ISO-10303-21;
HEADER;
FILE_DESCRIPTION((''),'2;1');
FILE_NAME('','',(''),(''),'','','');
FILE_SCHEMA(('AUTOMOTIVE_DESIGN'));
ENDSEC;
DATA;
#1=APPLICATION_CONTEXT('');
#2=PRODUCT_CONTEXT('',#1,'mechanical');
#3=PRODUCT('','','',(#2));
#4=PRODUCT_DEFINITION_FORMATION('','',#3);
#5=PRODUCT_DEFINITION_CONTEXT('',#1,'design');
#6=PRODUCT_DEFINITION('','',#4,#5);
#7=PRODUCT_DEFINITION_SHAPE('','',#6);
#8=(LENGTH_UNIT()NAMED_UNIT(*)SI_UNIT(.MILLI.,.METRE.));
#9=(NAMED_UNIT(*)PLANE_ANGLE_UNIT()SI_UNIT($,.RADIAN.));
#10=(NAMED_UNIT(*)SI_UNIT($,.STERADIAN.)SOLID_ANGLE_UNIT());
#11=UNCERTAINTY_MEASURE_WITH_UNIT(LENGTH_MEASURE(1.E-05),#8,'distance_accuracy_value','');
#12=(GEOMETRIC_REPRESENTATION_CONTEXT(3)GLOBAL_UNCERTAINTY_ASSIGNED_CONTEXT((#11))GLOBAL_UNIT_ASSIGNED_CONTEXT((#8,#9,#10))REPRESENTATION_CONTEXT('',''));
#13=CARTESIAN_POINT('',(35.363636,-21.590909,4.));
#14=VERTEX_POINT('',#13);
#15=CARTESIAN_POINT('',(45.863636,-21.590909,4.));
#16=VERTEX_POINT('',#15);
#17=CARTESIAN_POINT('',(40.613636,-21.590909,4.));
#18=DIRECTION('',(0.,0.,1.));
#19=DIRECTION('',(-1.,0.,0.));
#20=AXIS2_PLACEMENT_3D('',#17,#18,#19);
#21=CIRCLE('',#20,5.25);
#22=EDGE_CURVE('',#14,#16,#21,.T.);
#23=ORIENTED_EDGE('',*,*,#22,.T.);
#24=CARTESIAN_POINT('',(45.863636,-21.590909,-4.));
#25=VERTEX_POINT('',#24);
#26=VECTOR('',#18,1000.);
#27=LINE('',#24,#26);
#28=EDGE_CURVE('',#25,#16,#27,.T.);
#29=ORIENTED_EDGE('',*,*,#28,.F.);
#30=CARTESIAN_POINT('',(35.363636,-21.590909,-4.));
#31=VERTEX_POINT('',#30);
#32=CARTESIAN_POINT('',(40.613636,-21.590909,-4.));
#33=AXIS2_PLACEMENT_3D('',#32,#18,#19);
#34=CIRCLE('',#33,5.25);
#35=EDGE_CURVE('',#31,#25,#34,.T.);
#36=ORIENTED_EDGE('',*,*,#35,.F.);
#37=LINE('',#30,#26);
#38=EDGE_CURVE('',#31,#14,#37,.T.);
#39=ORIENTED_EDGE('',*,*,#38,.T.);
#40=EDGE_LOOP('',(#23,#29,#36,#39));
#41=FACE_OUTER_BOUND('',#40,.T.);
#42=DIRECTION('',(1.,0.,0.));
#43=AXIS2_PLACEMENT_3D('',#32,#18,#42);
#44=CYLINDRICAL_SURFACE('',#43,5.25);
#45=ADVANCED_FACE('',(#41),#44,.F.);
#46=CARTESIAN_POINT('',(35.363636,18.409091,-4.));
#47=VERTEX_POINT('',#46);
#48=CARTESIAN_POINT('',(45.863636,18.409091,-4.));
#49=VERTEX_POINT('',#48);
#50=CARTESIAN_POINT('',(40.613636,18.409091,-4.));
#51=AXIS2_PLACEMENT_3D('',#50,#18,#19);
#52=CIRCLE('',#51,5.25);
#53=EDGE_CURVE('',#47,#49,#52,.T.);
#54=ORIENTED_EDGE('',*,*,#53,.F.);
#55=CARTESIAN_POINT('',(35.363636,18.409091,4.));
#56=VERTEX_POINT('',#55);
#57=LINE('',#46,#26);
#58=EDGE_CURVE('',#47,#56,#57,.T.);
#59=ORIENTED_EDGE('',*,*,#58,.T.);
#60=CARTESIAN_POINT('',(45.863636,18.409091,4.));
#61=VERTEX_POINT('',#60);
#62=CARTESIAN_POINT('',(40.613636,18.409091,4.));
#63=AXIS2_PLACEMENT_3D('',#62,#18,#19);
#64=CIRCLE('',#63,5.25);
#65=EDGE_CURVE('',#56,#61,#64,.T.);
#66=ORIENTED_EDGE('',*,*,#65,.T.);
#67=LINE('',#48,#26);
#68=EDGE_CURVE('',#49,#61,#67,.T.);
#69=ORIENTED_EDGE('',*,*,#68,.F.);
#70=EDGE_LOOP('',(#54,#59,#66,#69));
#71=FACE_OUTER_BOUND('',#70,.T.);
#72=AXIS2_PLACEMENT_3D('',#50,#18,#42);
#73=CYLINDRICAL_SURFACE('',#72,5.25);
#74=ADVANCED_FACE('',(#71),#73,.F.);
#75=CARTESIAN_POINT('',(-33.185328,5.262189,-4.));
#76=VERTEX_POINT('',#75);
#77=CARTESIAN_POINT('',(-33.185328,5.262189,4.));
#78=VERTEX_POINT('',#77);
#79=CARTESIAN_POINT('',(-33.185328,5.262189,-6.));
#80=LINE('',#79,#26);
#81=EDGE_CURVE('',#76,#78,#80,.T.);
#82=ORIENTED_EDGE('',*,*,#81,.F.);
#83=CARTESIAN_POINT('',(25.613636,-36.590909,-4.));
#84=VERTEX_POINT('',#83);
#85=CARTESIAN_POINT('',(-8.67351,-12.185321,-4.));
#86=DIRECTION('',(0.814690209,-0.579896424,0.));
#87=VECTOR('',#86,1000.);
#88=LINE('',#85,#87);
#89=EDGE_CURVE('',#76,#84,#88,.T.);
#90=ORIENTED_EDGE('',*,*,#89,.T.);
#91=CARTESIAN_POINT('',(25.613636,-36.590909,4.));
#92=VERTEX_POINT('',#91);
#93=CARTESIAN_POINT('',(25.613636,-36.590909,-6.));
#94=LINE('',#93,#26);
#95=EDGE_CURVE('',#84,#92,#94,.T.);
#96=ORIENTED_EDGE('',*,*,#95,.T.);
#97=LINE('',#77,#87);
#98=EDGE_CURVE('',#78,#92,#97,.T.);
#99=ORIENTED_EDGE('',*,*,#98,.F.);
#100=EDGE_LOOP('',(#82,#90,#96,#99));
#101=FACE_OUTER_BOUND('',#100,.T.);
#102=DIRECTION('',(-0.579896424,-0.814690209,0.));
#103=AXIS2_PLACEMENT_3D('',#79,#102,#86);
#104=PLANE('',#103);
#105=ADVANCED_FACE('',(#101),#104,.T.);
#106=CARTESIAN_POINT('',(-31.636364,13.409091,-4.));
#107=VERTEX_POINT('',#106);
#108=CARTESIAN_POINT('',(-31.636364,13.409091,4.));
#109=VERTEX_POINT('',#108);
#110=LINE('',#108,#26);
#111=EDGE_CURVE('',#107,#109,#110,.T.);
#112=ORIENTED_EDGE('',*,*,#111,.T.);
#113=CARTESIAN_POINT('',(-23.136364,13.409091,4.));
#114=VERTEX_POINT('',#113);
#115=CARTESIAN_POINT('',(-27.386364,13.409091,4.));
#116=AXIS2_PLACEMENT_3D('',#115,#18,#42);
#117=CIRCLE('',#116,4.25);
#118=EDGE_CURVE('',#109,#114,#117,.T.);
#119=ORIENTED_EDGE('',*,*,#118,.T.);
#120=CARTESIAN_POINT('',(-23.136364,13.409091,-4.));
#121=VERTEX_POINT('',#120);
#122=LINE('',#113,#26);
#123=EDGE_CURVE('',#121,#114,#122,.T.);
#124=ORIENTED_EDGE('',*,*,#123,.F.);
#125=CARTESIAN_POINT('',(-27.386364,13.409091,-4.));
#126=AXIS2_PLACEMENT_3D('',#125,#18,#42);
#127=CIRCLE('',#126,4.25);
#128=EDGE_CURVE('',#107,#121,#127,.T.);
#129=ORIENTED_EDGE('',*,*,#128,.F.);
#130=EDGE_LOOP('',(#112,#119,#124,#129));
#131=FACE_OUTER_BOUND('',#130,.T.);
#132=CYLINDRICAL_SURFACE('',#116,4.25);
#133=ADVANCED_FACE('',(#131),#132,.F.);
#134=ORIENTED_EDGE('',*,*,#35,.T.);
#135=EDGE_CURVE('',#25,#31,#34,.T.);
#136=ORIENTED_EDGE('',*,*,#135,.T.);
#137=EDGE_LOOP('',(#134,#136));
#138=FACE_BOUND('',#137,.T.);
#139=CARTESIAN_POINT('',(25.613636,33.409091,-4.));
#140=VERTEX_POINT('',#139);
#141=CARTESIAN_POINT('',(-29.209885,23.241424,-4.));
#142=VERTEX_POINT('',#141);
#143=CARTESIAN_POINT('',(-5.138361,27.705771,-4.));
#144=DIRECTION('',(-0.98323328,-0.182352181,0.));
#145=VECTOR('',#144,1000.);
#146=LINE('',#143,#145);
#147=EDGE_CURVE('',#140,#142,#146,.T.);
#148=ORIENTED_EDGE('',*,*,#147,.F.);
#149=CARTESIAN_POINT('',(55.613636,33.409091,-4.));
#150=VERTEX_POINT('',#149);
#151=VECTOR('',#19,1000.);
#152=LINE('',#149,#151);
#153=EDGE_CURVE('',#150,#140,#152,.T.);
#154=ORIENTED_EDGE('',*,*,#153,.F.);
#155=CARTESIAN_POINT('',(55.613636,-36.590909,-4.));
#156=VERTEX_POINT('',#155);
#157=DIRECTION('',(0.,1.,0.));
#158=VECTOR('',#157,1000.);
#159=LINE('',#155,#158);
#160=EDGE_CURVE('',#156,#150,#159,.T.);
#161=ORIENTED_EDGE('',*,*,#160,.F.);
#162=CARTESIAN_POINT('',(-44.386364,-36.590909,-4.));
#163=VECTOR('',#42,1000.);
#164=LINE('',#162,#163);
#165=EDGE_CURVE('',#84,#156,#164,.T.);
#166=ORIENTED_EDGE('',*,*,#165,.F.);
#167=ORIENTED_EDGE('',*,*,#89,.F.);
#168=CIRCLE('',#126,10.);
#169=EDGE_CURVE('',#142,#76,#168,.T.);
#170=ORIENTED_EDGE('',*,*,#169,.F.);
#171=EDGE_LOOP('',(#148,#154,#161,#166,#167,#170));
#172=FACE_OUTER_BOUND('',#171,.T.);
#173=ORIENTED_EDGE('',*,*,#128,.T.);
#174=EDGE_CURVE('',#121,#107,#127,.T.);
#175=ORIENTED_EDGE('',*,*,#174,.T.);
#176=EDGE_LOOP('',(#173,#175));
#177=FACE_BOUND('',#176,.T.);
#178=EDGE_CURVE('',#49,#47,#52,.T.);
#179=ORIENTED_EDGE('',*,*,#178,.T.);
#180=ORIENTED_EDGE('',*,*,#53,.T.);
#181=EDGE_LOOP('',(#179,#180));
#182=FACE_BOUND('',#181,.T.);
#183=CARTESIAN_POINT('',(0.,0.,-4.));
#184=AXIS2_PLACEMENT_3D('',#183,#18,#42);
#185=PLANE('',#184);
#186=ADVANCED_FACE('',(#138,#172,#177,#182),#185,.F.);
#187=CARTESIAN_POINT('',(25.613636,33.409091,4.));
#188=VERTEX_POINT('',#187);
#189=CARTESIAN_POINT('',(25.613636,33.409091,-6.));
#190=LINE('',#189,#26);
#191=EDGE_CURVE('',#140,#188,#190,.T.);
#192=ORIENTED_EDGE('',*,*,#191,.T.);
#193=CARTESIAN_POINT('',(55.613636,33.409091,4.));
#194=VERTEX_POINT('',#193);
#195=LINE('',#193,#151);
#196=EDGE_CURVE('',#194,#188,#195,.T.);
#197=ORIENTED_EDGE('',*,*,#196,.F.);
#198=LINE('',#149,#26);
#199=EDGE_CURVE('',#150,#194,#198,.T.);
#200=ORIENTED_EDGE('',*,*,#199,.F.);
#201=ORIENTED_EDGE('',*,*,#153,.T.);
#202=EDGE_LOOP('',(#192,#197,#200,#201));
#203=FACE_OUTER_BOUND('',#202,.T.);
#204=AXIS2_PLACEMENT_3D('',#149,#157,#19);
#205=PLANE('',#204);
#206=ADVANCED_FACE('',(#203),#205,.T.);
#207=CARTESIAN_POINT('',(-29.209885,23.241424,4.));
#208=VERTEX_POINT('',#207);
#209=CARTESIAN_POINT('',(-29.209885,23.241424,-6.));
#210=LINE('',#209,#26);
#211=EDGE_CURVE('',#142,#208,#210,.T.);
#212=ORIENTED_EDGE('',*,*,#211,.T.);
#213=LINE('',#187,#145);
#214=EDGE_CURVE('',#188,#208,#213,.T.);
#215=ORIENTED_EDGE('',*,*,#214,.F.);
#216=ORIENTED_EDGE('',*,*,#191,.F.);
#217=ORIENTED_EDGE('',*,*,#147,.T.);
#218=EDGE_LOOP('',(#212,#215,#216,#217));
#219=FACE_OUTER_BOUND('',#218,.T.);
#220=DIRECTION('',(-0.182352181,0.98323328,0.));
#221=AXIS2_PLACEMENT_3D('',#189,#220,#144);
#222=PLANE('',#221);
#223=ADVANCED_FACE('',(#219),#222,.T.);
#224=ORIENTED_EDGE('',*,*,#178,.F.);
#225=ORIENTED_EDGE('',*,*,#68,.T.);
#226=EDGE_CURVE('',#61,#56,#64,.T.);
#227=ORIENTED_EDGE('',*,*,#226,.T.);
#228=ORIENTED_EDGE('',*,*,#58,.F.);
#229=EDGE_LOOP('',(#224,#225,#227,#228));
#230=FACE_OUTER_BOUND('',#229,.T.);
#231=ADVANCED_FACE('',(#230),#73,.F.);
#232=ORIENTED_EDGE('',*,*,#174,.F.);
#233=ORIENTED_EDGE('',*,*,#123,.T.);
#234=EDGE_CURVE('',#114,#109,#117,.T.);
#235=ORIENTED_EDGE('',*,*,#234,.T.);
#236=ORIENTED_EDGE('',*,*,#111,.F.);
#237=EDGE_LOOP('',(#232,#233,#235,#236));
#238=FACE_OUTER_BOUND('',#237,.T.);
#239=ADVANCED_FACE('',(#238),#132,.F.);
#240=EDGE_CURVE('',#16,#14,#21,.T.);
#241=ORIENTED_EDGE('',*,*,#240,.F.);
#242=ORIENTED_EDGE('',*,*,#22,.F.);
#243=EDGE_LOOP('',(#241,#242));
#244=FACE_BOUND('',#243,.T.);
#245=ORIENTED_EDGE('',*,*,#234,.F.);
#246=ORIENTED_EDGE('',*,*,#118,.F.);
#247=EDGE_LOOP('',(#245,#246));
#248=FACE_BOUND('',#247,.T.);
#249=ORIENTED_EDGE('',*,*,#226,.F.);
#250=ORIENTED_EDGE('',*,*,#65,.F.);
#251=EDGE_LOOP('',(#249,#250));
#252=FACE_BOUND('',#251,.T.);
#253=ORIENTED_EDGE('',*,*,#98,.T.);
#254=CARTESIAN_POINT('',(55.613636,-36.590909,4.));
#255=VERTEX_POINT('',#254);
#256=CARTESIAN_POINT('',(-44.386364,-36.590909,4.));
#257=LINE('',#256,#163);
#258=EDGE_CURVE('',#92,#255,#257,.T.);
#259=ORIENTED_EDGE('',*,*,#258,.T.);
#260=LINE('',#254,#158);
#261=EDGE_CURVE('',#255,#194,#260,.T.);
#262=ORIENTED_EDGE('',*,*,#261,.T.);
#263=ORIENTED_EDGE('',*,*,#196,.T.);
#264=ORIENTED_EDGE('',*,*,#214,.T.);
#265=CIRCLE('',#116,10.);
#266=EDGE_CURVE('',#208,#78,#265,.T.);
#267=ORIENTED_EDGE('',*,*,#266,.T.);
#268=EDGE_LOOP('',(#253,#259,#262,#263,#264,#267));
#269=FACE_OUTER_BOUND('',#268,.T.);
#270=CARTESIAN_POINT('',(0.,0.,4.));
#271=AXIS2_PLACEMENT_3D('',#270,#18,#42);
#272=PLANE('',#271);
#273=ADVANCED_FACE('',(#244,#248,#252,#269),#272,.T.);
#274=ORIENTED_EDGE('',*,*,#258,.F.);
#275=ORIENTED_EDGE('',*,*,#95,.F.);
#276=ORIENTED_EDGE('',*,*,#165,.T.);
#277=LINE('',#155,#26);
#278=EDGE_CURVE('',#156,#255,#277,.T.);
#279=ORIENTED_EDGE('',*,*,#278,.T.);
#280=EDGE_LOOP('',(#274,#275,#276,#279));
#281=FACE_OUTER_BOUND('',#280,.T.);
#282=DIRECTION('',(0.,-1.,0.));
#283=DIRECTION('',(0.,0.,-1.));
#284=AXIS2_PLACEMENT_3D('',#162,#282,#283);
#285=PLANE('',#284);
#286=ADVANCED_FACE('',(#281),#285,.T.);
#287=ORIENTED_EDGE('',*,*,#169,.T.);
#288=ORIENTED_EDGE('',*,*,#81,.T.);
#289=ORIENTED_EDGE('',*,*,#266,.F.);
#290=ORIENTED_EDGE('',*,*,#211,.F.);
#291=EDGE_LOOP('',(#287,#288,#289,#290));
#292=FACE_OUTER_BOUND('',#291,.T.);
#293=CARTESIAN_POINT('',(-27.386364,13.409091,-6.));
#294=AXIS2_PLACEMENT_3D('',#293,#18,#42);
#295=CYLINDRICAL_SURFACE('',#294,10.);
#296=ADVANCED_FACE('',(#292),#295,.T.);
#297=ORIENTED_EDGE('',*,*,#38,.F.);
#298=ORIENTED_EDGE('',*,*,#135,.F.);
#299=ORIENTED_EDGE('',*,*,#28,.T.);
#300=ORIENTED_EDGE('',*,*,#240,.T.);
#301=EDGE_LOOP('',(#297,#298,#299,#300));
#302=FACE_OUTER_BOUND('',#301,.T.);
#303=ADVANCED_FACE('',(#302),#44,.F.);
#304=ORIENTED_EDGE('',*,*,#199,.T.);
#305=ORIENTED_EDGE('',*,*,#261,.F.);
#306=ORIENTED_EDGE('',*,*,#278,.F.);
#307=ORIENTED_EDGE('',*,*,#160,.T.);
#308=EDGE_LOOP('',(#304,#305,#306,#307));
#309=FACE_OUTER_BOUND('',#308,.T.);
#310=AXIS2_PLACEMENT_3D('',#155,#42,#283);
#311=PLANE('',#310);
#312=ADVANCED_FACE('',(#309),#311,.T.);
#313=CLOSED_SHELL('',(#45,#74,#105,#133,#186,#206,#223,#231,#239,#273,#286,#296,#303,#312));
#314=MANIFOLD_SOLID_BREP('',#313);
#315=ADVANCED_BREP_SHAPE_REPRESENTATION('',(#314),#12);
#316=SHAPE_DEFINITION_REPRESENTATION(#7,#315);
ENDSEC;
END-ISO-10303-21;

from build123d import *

# Parameters (mm, degrees)
SKETCH1_W              = 100
SKETCH1_H              = 70
SKETCH1_R              = 5.25
BOSS_EXTRUDE1_DEPTH    = 8
SKETCH2_OUTSIDE_W      = 126.466
SKETCH2_OUTSIDE_H      = 96.466
CUT_EXTRUDE1_DEPTH     = 10
M10_TAPPED_HOLE1_D     = 8.5
M10_TAPPED_HOLE1_DEPTH = 24.5
M10_TAPPED_HOLE1_TIP   = 2.553657631


with BuildPart() as part:
    # Sketch1 → Boss-Extrude1 (new body)
    with BuildSketch(Plane.XY.offset(4)):
        with Locations((5.613636364, -1.590909091)):
            Rectangle(SKETCH1_W, SKETCH1_H)
        with Locations(Location((40.613636364, -21.590909091, 0), (0, 0, 180))):
            Circle(SKETCH1_R, mode=Mode.SUBTRACT)
        with Locations(Location((40.613636364, 18.409090909, 0), (0, 0, 180))):
            Circle(SKETCH1_R, mode=Mode.SUBTRACT)
    extrude(amount=-BOSS_EXTRUDE1_DEPTH)

    # Sketch2 outside → Cut-Extrude1 (cut)
    with BuildSketch(Plane.XY.offset(4)):
        with Locations((5.614, -1.591)):
            Rectangle(SKETCH2_OUTSIDE_W, SKETCH2_OUTSIDE_H)
        with BuildLine():
            Line((25.613636364, 33.409090909), (-29.209885446, 23.241423705))
            ThreePointArc((-29.209885446, 23.241423705), (-37.150522341, 15.56807326), (-33.185327877, 5.262188814))
            Line((-33.185327877, 5.262188814), (25.613636364, -36.590909091))
            Line((25.613636364, -36.590909091), (55.613636364, -36.590909091))
            Line((55.613636364, -36.590909091), (55.613636364, 33.409090909))
            Line((55.613636364, 33.409090909), (25.613636364, 33.409090909))
        make_face(mode=Mode.SUBTRACT)
    extrude(amount=-CUT_EXTRUDE1_DEPTH, mode=Mode.SUBTRACT)

    # M10 Tapped Hole1
    with Locations(Plane.XY.offset(4)):
        with Locations((-27.386363636, 13.409090909)):
            Hole(M10_TAPPED_HOLE1_D / 2, depth=M10_TAPPED_HOLE1_DEPTH)
            with Locations((0, 0, -(M10_TAPPED_HOLE1_DEPTH + M10_TAPPED_HOLE1_TIP / 2))):  # 118° drill point
                Cone(0, M10_TAPPED_HOLE1_D / 2, M10_TAPPED_HOLE1_TIP, mode=Mode.SUBTRACT)


solid = part.part
